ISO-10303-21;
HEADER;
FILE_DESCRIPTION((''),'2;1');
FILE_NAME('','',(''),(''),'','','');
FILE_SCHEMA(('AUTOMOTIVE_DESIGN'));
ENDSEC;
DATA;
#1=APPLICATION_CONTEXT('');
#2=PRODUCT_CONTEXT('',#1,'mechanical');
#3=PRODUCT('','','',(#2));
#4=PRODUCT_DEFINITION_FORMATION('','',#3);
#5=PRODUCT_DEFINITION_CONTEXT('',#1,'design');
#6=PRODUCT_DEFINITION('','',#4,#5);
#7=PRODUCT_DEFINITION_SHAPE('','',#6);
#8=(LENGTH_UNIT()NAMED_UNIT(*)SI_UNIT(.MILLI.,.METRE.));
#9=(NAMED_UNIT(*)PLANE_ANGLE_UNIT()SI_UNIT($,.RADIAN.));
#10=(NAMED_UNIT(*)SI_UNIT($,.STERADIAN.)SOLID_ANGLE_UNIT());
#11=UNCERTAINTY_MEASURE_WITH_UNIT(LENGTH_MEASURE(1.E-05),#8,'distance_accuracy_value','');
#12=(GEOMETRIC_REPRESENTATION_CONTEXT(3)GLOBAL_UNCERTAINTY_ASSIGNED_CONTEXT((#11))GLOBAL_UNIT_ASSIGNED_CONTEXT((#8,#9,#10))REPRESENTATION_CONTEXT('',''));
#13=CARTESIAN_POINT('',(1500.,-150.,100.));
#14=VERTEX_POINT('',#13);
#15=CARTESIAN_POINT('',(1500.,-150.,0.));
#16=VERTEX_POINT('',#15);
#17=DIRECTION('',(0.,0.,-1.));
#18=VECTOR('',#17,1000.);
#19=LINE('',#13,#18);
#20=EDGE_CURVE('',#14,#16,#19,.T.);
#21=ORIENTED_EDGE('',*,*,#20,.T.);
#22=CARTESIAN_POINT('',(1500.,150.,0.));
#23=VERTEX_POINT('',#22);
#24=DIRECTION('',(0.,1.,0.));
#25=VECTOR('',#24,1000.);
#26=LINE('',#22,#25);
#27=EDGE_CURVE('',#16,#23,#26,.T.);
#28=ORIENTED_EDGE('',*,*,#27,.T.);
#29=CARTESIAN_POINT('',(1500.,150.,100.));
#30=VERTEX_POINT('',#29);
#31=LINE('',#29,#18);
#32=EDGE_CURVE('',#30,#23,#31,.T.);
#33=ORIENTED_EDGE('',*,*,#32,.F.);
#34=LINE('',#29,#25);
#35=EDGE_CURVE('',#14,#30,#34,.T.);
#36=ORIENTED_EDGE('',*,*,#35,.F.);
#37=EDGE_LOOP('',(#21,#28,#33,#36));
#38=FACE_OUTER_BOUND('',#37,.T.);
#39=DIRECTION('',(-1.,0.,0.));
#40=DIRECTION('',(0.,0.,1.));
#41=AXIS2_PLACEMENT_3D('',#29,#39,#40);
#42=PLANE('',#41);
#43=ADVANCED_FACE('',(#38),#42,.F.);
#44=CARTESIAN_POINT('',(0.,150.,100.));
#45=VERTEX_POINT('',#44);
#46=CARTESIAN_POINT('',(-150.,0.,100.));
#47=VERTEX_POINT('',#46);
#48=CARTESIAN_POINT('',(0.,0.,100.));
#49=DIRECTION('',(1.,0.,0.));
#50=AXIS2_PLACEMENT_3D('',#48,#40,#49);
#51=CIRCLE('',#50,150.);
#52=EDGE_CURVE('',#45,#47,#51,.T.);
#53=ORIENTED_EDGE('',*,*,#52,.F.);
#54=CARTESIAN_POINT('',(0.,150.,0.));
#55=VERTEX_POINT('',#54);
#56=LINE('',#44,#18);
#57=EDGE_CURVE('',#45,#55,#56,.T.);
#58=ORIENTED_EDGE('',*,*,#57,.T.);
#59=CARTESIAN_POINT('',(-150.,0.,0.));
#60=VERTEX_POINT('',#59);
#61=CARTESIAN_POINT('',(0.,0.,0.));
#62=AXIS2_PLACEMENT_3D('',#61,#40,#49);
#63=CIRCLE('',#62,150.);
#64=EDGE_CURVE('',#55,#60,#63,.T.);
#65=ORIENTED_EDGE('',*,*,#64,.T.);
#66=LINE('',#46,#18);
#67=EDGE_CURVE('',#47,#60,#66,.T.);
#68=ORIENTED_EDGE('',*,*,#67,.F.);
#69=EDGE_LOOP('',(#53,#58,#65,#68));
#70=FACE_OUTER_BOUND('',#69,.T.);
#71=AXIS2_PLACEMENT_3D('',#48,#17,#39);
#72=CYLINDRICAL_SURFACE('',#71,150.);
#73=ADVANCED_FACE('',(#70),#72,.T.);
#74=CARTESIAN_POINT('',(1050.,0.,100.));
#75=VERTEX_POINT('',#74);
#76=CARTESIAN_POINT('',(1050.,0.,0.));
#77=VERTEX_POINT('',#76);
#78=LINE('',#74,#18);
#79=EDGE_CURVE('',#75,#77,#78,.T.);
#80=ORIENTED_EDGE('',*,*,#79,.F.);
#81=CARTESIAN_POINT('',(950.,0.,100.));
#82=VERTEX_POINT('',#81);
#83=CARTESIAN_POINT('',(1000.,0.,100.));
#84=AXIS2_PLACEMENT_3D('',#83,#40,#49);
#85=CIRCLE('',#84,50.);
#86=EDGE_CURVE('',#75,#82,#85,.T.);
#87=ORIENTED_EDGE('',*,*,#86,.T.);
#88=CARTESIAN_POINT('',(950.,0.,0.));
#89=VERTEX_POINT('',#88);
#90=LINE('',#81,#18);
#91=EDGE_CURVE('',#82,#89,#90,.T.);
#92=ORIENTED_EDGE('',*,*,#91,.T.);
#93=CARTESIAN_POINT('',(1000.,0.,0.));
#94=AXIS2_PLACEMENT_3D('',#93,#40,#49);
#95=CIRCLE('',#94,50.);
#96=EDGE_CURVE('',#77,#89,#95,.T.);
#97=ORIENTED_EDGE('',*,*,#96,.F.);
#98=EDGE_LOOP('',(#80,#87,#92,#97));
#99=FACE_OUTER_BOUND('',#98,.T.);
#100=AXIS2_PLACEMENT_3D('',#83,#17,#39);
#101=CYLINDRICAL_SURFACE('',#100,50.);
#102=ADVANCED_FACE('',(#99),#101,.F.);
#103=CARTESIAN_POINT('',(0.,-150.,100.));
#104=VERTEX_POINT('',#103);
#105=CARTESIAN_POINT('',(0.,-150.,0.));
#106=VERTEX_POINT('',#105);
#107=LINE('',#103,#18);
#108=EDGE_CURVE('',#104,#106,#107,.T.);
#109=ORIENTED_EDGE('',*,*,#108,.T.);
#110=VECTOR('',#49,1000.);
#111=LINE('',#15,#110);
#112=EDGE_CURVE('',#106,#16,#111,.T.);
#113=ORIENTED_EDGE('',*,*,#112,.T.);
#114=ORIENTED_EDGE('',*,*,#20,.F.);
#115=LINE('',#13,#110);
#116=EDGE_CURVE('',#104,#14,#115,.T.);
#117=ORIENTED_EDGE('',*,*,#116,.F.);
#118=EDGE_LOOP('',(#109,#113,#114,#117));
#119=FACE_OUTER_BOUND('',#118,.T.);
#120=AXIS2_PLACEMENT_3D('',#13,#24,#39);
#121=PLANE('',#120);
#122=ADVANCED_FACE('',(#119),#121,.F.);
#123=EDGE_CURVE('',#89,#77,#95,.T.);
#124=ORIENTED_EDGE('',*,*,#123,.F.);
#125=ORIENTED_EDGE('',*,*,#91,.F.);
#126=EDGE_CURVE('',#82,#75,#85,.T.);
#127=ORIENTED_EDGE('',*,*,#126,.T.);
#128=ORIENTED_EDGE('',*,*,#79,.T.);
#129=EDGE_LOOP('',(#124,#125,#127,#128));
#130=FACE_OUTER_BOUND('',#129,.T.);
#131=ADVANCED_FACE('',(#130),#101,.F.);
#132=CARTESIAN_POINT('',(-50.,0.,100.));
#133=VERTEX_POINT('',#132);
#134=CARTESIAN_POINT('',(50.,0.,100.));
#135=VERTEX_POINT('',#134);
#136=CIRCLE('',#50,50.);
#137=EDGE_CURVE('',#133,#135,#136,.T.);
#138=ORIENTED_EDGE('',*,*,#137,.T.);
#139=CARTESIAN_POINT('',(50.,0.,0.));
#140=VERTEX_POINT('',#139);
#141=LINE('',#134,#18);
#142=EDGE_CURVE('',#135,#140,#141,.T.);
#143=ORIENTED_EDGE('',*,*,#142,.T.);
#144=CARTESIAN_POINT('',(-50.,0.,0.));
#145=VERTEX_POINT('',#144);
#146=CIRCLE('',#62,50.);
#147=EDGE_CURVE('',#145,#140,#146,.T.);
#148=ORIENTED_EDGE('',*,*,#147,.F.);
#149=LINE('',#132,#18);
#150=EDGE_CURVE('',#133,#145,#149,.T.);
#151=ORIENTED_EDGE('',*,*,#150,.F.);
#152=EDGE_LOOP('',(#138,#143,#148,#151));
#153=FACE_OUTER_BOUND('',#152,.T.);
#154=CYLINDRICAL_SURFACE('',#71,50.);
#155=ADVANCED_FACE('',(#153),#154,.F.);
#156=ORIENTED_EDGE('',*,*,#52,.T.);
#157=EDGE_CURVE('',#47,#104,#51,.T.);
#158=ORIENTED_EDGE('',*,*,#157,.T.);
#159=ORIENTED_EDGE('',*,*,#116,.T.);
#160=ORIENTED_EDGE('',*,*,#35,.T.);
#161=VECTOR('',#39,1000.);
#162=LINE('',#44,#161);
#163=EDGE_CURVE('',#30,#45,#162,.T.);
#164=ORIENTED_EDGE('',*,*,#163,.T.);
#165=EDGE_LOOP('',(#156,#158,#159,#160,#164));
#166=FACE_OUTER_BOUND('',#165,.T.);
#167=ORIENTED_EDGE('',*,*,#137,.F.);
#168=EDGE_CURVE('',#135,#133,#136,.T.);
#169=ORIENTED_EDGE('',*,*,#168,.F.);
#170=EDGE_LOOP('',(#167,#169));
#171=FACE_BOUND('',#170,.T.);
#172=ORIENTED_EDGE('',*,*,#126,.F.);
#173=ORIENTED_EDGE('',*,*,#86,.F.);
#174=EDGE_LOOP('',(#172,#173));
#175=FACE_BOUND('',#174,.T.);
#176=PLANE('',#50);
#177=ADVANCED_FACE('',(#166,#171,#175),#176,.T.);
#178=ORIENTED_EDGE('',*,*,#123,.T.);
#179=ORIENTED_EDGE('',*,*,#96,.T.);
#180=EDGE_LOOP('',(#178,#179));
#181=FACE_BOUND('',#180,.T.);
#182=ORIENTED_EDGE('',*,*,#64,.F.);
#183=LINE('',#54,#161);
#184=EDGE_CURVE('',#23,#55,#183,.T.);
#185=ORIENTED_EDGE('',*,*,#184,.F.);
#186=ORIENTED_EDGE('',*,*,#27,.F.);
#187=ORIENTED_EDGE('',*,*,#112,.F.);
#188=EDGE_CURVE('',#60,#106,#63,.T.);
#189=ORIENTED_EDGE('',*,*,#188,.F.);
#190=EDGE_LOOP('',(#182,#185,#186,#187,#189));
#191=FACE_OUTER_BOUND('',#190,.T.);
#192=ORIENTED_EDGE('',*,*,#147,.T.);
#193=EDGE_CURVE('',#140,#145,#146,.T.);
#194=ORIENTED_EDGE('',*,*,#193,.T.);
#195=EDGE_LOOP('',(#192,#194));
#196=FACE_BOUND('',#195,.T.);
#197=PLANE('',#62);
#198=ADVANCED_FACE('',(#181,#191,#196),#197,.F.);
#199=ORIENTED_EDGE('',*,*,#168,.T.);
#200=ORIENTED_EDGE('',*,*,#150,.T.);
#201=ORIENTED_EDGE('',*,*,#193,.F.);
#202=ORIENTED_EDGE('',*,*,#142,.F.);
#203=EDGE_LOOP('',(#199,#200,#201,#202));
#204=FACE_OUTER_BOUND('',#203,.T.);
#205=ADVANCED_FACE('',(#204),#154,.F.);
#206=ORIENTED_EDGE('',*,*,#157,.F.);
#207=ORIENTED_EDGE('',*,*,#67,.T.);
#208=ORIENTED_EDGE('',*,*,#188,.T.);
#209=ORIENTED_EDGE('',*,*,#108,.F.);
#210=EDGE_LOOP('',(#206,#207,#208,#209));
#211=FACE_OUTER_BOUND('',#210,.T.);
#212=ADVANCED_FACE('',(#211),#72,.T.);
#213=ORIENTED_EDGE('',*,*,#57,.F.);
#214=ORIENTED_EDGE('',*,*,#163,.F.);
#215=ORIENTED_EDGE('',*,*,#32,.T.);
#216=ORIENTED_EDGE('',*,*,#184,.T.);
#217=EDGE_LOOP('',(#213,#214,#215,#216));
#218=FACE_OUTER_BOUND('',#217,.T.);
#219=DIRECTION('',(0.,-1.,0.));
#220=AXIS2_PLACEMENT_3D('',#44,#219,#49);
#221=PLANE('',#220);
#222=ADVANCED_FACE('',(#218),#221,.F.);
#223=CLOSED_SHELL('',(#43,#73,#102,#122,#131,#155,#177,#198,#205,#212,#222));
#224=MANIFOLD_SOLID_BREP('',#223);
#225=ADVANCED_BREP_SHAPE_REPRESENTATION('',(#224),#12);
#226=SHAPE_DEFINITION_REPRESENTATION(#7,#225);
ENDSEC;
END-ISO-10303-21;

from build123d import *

# Parameters (mm, degrees)
SKETCH1_R           = 50
BOSS_EXTRUDE1_DEPTH = 100


with BuildPart() as part:
    # Sketch1 → Boss-Extrude1 (new body)
    with BuildSketch(Plane.XY):
        with BuildLine():
            Line((0, 150), (1500, 150))
            Line((1500, 150), (1500, -150))
            Line((1500, -150), (0, -150))
            ThreePointArc((0, -150), (-150, 0), (0, 150))
        make_face()
        with Locations((1000, 0)):
            Circle(SKETCH1_R, mode=Mode.SUBTRACT)
        Circle(SKETCH1_R, mode=Mode.SUBTRACT)
    extrude(amount=BOSS_EXTRUDE1_DEPTH)


solid = part.part
